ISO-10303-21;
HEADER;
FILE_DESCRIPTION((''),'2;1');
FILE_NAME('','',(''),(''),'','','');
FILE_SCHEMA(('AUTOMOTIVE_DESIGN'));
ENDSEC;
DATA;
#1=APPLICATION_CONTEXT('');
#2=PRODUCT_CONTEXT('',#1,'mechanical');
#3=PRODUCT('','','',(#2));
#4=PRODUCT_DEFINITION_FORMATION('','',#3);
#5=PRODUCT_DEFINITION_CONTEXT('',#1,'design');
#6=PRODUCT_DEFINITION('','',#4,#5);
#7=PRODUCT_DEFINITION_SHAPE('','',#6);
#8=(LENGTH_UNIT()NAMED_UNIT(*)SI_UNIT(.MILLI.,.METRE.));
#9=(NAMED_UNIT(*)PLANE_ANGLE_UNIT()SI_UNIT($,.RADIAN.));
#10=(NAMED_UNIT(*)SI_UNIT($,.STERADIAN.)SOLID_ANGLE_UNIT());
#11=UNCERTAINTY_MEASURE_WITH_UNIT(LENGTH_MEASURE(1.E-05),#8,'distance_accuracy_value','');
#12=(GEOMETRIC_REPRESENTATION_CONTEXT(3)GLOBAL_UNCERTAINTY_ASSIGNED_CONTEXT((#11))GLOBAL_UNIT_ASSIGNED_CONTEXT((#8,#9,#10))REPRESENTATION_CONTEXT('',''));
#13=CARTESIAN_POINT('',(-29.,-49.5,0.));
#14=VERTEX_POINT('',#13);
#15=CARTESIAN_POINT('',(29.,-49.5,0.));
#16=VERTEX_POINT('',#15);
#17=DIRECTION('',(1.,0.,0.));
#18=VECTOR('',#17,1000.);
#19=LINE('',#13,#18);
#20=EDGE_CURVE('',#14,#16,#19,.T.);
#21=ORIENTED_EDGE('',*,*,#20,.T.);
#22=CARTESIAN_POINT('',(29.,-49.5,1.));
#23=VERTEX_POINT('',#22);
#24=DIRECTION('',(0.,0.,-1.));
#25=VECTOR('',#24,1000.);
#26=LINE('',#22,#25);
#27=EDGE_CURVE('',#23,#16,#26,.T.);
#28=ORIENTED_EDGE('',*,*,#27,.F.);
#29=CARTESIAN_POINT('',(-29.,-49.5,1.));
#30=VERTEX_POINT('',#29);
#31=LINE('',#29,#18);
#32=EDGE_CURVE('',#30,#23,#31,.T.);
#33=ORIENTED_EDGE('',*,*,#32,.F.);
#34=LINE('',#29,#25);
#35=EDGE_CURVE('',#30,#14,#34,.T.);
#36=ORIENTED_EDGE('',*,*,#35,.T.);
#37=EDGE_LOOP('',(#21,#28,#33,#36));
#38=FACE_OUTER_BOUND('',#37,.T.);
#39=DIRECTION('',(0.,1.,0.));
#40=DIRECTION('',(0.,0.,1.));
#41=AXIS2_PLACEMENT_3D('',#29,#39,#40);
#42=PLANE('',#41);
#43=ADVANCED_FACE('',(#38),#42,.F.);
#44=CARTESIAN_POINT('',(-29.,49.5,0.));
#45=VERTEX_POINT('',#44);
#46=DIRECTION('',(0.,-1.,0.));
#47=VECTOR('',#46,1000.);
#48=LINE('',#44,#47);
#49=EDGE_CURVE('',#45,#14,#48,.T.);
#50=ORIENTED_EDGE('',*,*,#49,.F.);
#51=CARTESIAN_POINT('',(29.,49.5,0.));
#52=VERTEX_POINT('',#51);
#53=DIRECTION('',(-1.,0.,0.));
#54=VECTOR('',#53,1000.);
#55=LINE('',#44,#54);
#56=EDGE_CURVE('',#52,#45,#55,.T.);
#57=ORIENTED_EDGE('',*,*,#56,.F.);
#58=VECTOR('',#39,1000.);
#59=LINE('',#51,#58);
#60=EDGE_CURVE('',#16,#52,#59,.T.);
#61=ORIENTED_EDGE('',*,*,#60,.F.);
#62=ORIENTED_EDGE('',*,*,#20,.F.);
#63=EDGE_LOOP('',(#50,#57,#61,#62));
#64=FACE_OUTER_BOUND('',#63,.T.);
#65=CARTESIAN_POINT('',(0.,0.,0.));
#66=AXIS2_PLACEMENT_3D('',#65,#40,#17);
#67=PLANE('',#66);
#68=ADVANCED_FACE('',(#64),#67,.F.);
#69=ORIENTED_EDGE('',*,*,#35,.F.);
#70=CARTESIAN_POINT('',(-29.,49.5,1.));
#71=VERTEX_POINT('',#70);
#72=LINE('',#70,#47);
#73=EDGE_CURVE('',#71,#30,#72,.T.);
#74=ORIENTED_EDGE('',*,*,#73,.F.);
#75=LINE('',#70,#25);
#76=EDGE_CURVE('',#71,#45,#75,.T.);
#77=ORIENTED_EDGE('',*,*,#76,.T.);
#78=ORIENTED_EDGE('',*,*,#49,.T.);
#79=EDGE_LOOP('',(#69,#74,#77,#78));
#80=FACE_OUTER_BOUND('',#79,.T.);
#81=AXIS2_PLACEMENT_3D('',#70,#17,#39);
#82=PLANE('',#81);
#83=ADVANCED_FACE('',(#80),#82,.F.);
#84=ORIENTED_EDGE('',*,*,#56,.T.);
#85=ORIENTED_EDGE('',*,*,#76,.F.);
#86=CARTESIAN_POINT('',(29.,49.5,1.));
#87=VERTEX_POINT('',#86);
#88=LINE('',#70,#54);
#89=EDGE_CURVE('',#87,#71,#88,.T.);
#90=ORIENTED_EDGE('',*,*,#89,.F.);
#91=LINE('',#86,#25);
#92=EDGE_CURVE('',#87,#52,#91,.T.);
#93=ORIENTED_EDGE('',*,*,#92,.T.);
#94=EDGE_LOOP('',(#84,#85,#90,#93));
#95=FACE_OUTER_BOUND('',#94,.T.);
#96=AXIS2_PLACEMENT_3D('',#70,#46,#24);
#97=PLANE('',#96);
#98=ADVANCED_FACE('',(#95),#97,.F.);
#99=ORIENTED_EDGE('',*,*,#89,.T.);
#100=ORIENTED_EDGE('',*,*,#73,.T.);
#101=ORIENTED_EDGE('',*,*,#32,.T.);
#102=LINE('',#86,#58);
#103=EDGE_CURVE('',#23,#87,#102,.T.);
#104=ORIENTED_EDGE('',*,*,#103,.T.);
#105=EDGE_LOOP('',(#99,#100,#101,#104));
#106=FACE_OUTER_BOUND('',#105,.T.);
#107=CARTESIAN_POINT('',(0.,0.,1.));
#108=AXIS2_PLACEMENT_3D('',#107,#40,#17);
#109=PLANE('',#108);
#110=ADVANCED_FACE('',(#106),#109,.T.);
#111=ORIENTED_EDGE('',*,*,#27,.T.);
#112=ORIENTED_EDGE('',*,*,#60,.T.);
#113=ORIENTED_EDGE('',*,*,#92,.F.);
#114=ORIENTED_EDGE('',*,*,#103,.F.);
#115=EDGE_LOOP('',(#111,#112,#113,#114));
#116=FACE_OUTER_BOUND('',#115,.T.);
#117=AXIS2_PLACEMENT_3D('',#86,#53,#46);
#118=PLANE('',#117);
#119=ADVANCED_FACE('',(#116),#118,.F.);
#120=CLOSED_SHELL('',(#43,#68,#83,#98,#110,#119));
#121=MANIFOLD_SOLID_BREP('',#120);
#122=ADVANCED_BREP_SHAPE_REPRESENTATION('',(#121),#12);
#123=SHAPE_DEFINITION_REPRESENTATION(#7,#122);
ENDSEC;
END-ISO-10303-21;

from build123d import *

# Parameters (mm, degrees)
SKETCH1_W           = 58
SKETCH1_H           = 99
BOSS_EXTRUDE1_DEPTH = 1


with BuildPart() as part:
    # Sketch1 → Boss-Extrude1 (new body)
    with BuildSketch(Plane.XY):
        Rectangle(SKETCH1_W, SKETCH1_H)
    extrude(amount=BOSS_EXTRUDE1_DEPTH)


solid = part.part
